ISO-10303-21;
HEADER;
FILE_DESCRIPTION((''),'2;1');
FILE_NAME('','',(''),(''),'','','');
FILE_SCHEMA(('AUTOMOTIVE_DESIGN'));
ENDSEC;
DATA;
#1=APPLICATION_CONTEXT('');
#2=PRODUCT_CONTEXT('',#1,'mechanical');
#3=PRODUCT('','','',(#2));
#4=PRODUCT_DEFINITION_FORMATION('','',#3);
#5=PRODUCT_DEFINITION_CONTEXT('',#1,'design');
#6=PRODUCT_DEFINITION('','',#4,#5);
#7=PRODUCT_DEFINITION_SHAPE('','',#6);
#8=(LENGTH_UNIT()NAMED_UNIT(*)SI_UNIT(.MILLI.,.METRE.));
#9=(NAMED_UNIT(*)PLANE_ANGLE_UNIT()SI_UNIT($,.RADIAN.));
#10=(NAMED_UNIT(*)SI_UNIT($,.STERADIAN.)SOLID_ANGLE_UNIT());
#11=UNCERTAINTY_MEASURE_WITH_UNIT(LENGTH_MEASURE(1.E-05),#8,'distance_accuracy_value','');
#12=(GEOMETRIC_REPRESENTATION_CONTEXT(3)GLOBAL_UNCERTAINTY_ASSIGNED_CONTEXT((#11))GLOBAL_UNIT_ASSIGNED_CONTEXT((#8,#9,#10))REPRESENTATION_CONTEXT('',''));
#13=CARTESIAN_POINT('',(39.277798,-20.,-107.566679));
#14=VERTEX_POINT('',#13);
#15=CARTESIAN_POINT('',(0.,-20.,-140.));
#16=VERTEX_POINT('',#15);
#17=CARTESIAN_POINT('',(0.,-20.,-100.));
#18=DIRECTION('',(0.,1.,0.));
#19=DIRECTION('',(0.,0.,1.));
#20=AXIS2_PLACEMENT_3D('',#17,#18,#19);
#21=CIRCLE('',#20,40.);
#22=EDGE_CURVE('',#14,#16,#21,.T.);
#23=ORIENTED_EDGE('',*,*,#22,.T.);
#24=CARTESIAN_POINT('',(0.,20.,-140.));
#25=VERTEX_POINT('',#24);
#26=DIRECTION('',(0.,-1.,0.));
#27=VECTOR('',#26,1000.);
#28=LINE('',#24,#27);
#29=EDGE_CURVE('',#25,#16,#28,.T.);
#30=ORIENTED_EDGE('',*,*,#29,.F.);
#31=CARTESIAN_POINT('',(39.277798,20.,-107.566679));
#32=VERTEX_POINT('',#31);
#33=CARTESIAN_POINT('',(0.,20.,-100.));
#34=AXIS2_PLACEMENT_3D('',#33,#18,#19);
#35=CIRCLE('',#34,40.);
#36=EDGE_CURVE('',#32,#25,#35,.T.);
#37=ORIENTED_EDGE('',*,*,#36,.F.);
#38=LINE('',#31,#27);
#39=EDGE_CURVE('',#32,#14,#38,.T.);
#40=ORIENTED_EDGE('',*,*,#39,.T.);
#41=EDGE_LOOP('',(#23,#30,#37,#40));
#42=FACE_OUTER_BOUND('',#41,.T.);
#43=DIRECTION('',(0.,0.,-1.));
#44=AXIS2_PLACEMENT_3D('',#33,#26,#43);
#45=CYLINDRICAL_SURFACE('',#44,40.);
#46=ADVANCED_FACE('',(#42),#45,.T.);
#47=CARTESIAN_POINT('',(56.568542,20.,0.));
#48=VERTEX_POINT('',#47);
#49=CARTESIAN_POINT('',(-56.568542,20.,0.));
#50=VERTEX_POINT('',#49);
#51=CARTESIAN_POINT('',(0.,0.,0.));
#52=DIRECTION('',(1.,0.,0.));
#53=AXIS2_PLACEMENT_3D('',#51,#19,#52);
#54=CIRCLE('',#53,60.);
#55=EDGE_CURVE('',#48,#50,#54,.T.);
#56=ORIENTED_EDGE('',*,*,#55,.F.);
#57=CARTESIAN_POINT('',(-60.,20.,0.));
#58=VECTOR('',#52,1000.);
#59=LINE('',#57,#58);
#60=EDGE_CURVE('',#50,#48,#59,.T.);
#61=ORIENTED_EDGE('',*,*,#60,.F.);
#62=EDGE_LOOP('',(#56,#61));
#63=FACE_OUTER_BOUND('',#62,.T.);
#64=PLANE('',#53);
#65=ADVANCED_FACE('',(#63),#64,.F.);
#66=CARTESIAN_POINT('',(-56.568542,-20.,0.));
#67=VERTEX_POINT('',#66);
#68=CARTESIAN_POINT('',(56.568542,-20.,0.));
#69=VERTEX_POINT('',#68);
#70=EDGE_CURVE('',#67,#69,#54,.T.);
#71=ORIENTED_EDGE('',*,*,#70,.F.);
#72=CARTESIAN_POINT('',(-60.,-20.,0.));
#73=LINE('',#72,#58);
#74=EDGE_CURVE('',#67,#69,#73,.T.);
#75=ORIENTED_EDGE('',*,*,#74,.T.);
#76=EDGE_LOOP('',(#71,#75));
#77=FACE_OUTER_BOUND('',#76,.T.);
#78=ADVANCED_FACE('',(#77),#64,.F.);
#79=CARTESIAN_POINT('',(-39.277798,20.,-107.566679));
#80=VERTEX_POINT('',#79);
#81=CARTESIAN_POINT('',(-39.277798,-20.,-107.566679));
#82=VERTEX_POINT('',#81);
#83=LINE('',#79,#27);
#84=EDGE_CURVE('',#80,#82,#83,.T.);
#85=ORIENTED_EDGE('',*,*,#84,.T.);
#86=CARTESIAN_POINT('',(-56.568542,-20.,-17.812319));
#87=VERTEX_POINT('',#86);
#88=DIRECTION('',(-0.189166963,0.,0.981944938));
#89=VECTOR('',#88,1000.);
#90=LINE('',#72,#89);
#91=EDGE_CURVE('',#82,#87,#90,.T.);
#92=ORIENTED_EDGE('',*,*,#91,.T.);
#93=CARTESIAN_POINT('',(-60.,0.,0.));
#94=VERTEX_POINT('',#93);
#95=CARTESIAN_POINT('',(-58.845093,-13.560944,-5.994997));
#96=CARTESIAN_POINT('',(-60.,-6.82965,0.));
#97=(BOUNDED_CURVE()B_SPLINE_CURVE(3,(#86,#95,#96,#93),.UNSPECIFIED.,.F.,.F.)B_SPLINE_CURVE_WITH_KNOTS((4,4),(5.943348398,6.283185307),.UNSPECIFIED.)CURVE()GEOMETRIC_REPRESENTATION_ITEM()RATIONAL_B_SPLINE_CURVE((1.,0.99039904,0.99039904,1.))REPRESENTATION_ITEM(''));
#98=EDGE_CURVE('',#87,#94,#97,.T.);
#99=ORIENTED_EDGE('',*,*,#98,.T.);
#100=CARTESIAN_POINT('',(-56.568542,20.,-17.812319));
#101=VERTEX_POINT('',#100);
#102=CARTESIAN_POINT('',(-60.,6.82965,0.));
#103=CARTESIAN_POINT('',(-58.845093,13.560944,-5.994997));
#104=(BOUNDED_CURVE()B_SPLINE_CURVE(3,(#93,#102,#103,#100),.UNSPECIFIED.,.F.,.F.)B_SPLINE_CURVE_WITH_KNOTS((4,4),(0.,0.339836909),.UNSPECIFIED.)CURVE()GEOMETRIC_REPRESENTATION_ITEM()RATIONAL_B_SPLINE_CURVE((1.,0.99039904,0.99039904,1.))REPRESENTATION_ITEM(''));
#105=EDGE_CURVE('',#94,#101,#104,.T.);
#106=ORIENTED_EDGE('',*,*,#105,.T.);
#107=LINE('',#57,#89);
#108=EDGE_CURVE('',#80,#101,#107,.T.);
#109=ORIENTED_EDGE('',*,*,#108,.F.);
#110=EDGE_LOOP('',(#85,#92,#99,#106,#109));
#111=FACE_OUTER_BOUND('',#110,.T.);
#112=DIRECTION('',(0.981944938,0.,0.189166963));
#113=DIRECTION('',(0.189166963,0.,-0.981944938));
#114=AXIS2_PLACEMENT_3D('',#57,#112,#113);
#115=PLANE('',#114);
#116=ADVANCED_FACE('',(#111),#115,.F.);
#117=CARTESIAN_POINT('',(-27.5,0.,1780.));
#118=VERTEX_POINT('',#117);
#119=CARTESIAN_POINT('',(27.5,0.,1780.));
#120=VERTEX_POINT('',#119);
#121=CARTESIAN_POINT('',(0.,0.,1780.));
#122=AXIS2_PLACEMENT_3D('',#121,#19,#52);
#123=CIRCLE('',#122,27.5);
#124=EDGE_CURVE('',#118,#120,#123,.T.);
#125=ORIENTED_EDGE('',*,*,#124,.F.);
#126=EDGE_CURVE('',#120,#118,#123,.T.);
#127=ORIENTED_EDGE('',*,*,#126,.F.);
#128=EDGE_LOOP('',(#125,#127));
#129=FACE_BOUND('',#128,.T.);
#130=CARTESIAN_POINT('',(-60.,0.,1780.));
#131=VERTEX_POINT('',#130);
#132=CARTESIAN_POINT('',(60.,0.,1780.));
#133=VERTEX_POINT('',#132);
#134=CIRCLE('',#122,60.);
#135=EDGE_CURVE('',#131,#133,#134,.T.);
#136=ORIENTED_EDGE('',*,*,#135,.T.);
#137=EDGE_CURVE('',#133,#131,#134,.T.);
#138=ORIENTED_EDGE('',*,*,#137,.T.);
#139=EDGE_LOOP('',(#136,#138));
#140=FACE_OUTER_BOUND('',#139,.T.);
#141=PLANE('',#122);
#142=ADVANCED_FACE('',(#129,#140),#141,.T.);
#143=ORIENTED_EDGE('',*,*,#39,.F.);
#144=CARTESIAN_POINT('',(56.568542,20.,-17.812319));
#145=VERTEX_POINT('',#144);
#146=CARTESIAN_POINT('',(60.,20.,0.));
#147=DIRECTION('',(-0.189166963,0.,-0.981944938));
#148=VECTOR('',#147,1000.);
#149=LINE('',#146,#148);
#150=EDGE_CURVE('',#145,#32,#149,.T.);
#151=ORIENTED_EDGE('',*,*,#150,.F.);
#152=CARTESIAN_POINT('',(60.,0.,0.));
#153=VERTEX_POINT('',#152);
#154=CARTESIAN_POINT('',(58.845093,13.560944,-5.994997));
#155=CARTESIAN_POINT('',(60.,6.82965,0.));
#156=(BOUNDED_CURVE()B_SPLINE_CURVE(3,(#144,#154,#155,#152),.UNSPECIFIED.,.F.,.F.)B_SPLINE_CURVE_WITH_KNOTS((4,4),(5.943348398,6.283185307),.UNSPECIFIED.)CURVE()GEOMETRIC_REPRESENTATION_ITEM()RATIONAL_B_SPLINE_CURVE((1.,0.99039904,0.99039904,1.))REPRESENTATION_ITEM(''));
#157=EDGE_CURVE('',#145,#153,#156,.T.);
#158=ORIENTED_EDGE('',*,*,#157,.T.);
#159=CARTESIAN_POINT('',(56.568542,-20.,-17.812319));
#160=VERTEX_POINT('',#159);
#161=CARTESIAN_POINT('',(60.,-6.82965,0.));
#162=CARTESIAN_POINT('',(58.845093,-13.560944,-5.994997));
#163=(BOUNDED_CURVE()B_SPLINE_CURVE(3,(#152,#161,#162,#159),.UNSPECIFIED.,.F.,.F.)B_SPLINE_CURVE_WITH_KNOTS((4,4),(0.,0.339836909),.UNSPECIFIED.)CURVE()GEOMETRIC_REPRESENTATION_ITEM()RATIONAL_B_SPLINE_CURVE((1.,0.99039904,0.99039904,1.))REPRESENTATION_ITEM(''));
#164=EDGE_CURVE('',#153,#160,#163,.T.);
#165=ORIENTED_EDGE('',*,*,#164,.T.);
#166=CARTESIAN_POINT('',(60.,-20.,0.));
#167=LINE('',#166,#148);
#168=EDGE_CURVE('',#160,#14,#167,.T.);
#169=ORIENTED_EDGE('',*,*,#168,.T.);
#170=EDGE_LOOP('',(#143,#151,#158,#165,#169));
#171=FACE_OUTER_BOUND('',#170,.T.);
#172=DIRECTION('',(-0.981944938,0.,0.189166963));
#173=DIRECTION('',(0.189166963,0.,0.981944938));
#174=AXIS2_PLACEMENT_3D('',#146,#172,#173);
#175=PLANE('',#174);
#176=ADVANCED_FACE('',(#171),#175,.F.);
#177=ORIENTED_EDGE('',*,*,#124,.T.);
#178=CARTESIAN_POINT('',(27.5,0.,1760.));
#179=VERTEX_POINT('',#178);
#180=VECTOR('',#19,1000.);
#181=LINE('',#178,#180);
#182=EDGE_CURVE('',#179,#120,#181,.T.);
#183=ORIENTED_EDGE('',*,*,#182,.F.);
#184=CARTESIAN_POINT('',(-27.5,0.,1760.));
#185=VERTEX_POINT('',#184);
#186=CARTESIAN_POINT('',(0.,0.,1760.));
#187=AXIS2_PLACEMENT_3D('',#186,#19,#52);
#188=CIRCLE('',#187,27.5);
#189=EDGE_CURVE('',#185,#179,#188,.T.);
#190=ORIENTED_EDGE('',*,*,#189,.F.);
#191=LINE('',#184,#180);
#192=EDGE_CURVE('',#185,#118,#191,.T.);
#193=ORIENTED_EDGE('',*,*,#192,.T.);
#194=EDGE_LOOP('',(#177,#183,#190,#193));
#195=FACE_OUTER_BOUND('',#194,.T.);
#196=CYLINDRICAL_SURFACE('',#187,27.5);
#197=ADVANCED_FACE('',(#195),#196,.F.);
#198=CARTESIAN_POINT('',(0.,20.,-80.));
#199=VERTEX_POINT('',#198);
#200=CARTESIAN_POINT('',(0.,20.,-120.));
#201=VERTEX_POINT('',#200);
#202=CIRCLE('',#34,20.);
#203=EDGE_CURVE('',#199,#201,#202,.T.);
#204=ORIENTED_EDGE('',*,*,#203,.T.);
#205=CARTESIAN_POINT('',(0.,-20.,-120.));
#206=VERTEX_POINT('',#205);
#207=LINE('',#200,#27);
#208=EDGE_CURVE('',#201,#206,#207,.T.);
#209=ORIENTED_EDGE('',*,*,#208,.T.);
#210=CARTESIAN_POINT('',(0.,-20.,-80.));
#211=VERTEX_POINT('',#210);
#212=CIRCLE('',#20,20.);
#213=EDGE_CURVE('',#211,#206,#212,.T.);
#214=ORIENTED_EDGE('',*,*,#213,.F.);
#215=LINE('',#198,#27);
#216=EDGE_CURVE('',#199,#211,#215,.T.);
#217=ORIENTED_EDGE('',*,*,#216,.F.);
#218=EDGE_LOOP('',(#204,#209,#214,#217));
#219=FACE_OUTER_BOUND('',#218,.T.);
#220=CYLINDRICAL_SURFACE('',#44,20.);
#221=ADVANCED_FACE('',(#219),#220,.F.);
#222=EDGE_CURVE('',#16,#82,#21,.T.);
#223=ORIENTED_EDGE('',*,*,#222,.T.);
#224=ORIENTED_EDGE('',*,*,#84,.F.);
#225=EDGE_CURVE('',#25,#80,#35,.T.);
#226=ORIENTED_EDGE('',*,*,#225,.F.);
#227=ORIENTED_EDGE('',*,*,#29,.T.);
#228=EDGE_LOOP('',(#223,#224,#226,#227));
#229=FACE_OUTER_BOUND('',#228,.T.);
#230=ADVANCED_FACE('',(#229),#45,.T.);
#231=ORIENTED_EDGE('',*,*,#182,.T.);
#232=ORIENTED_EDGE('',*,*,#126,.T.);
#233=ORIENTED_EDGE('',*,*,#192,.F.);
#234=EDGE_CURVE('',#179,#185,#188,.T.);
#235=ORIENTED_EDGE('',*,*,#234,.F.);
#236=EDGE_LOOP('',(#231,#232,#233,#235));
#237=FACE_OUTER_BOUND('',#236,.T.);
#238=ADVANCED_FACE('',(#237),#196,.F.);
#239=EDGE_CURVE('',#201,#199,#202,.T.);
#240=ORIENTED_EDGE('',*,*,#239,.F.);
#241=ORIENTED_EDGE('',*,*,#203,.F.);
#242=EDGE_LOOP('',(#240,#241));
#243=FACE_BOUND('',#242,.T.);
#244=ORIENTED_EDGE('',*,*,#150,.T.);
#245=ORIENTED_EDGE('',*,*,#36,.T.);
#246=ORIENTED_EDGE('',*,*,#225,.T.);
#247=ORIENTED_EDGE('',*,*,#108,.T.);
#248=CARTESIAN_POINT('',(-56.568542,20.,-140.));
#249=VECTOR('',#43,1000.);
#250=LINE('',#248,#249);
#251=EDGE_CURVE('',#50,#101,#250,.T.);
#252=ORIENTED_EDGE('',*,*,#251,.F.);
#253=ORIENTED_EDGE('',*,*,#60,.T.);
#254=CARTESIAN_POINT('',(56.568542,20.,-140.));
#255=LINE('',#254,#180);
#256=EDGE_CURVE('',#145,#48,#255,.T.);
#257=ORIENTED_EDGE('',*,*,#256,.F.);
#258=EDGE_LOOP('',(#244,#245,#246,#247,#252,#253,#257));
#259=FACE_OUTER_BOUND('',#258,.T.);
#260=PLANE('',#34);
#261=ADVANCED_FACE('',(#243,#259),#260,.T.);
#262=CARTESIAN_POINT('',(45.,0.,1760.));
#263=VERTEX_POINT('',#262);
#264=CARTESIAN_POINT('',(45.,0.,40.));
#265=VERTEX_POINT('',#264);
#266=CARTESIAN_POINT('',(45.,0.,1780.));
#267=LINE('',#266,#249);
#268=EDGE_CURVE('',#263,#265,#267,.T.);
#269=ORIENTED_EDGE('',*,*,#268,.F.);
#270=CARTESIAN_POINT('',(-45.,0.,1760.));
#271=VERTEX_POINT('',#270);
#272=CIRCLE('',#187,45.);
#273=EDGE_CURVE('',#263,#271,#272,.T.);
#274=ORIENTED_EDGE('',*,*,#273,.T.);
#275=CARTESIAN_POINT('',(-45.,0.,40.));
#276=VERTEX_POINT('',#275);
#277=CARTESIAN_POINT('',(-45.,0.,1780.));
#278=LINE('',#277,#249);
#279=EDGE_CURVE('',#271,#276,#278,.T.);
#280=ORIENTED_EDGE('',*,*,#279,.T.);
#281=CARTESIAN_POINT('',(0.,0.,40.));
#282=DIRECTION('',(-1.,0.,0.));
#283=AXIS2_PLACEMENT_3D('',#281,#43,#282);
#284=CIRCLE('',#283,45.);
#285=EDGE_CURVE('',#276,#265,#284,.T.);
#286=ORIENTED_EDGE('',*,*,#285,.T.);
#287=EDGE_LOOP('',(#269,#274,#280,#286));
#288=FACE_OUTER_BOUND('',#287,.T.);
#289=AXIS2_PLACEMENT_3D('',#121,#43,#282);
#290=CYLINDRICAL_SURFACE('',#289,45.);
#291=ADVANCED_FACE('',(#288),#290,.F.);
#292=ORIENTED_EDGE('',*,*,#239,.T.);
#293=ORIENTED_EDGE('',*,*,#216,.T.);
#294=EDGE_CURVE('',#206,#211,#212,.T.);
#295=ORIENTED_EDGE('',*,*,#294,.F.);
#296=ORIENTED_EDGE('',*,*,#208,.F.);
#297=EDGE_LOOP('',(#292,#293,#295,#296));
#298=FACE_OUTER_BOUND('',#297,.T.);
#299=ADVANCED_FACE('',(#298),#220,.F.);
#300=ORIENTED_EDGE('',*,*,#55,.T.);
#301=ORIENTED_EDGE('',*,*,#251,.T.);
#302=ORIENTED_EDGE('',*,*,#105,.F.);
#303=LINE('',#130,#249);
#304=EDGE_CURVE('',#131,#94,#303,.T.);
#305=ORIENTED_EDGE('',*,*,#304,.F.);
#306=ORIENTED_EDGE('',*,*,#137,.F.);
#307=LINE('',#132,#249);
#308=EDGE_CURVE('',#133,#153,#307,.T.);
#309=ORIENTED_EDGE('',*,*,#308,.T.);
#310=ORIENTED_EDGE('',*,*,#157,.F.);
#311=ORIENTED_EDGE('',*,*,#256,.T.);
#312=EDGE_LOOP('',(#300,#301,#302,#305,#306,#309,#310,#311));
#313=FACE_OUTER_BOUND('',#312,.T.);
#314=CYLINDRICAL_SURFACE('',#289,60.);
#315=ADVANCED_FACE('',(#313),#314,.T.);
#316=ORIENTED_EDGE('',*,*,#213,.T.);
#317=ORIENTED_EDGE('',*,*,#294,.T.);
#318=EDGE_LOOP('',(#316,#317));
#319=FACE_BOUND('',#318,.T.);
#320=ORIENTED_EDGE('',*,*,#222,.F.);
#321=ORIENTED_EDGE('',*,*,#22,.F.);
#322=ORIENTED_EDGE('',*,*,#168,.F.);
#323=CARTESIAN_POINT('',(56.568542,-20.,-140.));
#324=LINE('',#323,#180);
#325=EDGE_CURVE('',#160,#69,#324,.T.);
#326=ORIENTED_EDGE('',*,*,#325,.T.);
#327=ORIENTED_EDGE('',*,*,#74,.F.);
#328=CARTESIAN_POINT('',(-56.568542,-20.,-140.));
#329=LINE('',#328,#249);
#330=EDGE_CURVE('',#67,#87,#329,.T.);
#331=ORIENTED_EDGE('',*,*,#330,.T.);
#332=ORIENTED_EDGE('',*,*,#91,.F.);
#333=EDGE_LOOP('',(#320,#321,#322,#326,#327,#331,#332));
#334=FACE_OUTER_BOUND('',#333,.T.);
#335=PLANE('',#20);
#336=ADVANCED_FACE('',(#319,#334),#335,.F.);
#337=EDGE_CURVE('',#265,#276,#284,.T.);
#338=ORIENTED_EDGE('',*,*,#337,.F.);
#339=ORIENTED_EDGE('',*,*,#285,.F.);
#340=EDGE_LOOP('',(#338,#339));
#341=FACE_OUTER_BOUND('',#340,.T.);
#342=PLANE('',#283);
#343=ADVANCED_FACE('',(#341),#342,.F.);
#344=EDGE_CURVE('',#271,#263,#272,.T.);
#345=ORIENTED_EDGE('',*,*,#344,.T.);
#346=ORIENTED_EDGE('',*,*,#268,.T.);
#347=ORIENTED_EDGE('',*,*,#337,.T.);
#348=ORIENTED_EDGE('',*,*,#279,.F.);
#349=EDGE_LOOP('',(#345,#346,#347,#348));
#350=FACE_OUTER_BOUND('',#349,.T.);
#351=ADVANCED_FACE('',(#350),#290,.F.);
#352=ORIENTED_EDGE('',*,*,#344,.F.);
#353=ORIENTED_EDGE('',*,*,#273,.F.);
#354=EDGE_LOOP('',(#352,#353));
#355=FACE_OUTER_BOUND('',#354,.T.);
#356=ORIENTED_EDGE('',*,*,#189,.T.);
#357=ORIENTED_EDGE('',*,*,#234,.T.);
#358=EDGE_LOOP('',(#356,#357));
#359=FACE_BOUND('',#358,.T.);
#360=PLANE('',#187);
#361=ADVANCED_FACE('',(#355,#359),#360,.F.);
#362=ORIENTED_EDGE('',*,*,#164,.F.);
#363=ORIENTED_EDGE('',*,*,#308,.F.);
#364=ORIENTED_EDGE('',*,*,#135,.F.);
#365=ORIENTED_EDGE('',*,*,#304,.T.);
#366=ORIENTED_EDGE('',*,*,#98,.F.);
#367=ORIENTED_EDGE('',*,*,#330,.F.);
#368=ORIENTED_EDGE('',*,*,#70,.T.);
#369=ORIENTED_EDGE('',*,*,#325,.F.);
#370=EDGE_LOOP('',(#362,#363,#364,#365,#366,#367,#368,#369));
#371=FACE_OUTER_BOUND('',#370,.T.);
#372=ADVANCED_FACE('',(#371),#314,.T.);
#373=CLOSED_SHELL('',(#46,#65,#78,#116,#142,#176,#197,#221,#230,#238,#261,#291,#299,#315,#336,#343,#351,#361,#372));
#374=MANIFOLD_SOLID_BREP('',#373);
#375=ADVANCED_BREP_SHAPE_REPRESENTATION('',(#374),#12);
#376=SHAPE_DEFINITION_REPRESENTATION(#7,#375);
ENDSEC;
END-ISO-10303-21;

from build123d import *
from build123d.topology import SkipClean

# Parameters (mm, degrees)
SKETCH_1_R          = 60
SKETCH_1_R_2        = 45
EXTRUDE_1_DEPTH     = 1780
SKETCH_2_R          = 20
EXTRUDE_2_DEPTH     = 20
SKETCH_3_R          = 50
EXTRUDE_3_DEPTH     = 40
SKETCH_4_OUTSIDE_W  = 507.498
SKETCH_4_OUTSIDE_H  = 507.498
SKETCH_4_OUTSIDE_R  = 60
CUT_EXTRUDE_1_DEPTH = 1783.021324227
EXTRUDE_START       = -20
SKETCH_5_R          = 60
SKETCH_5_R_2        = 27.5
EXTRUDE_4_DEPTH     = 20


with BuildPart() as part:
    # 草图1 → 凸台-拉伸1 (new body)
    with BuildSketch(Plane.XY):
        Circle(SKETCH_1_R)
        Circle(SKETCH_1_R_2, mode=Mode.SUBTRACT)
    extrude(amount=EXTRUDE_1_DEPTH)

    # 草图2 → 凸台-拉伸2 (add, symmetric)
    with BuildSketch(Plane(origin=(0, 0, 0), x_dir=(1, 0, 0), z_dir=(0, 1, 0))):
        with BuildLine():
            Line((-60, 0), (-39.2777975, 107.5666785))
            ThreePointArc((-39.2777975, 107.5666785), (0, 140), (39.2777975, 107.5666785))
            Line((39.2777975, 107.5666785), (60, 0))
            Line((60, 0), (-60, 0))
        make_face()
        with Locations(Location((0, 100, 0), (0, 0, 270))):
            Circle(SKETCH_2_R, mode=Mode.SUBTRACT)
    extrude(amount=EXTRUDE_2_DEPTH, both=True)

    # 草图3 → 凸台-拉伸3 (add)
    with BuildSketch(Plane(origin=(0, 0, 0), x_dir=(-1, 0, 0), z_dir=(0, 0, -1))):
        Circle(SKETCH_3_R)
    extrude(amount=-EXTRUDE_3_DEPTH)

    # 草图4 outside → 切除-拉伸1 (cut, through all)
    with BuildSketch(Plane(origin=(0, 0, 0), x_dir=(-1, 0, 0), z_dir=(0, 0, -1))):
        Rectangle(SKETCH_4_OUTSIDE_W, SKETCH_4_OUTSIDE_H)
        with Locations(Location((0, 0, 0), (0, 0, 19.471220634))):
            Circle(SKETCH_4_OUTSIDE_R, mode=Mode.SUBTRACT)
    extrude(amount=CUT_EXTRUDE_1_DEPTH, mode=Mode.SUBTRACT)

    # 草图5 → 凸台-拉伸4 (add)
    with SkipClean():  # the faces are left unmerged after this step: merging them gives an invalid solid
        with BuildSketch(Plane.XY.offset(1780).offset(EXTRUDE_START)):
            with Locations(Location((0, 0, 0), (0, 0, 160.528779366))):
                Circle(SKETCH_5_R)
            Circle(SKETCH_5_R_2, mode=Mode.SUBTRACT)
        extrude(amount=EXTRUDE_4_DEPTH)


solid = part.part
